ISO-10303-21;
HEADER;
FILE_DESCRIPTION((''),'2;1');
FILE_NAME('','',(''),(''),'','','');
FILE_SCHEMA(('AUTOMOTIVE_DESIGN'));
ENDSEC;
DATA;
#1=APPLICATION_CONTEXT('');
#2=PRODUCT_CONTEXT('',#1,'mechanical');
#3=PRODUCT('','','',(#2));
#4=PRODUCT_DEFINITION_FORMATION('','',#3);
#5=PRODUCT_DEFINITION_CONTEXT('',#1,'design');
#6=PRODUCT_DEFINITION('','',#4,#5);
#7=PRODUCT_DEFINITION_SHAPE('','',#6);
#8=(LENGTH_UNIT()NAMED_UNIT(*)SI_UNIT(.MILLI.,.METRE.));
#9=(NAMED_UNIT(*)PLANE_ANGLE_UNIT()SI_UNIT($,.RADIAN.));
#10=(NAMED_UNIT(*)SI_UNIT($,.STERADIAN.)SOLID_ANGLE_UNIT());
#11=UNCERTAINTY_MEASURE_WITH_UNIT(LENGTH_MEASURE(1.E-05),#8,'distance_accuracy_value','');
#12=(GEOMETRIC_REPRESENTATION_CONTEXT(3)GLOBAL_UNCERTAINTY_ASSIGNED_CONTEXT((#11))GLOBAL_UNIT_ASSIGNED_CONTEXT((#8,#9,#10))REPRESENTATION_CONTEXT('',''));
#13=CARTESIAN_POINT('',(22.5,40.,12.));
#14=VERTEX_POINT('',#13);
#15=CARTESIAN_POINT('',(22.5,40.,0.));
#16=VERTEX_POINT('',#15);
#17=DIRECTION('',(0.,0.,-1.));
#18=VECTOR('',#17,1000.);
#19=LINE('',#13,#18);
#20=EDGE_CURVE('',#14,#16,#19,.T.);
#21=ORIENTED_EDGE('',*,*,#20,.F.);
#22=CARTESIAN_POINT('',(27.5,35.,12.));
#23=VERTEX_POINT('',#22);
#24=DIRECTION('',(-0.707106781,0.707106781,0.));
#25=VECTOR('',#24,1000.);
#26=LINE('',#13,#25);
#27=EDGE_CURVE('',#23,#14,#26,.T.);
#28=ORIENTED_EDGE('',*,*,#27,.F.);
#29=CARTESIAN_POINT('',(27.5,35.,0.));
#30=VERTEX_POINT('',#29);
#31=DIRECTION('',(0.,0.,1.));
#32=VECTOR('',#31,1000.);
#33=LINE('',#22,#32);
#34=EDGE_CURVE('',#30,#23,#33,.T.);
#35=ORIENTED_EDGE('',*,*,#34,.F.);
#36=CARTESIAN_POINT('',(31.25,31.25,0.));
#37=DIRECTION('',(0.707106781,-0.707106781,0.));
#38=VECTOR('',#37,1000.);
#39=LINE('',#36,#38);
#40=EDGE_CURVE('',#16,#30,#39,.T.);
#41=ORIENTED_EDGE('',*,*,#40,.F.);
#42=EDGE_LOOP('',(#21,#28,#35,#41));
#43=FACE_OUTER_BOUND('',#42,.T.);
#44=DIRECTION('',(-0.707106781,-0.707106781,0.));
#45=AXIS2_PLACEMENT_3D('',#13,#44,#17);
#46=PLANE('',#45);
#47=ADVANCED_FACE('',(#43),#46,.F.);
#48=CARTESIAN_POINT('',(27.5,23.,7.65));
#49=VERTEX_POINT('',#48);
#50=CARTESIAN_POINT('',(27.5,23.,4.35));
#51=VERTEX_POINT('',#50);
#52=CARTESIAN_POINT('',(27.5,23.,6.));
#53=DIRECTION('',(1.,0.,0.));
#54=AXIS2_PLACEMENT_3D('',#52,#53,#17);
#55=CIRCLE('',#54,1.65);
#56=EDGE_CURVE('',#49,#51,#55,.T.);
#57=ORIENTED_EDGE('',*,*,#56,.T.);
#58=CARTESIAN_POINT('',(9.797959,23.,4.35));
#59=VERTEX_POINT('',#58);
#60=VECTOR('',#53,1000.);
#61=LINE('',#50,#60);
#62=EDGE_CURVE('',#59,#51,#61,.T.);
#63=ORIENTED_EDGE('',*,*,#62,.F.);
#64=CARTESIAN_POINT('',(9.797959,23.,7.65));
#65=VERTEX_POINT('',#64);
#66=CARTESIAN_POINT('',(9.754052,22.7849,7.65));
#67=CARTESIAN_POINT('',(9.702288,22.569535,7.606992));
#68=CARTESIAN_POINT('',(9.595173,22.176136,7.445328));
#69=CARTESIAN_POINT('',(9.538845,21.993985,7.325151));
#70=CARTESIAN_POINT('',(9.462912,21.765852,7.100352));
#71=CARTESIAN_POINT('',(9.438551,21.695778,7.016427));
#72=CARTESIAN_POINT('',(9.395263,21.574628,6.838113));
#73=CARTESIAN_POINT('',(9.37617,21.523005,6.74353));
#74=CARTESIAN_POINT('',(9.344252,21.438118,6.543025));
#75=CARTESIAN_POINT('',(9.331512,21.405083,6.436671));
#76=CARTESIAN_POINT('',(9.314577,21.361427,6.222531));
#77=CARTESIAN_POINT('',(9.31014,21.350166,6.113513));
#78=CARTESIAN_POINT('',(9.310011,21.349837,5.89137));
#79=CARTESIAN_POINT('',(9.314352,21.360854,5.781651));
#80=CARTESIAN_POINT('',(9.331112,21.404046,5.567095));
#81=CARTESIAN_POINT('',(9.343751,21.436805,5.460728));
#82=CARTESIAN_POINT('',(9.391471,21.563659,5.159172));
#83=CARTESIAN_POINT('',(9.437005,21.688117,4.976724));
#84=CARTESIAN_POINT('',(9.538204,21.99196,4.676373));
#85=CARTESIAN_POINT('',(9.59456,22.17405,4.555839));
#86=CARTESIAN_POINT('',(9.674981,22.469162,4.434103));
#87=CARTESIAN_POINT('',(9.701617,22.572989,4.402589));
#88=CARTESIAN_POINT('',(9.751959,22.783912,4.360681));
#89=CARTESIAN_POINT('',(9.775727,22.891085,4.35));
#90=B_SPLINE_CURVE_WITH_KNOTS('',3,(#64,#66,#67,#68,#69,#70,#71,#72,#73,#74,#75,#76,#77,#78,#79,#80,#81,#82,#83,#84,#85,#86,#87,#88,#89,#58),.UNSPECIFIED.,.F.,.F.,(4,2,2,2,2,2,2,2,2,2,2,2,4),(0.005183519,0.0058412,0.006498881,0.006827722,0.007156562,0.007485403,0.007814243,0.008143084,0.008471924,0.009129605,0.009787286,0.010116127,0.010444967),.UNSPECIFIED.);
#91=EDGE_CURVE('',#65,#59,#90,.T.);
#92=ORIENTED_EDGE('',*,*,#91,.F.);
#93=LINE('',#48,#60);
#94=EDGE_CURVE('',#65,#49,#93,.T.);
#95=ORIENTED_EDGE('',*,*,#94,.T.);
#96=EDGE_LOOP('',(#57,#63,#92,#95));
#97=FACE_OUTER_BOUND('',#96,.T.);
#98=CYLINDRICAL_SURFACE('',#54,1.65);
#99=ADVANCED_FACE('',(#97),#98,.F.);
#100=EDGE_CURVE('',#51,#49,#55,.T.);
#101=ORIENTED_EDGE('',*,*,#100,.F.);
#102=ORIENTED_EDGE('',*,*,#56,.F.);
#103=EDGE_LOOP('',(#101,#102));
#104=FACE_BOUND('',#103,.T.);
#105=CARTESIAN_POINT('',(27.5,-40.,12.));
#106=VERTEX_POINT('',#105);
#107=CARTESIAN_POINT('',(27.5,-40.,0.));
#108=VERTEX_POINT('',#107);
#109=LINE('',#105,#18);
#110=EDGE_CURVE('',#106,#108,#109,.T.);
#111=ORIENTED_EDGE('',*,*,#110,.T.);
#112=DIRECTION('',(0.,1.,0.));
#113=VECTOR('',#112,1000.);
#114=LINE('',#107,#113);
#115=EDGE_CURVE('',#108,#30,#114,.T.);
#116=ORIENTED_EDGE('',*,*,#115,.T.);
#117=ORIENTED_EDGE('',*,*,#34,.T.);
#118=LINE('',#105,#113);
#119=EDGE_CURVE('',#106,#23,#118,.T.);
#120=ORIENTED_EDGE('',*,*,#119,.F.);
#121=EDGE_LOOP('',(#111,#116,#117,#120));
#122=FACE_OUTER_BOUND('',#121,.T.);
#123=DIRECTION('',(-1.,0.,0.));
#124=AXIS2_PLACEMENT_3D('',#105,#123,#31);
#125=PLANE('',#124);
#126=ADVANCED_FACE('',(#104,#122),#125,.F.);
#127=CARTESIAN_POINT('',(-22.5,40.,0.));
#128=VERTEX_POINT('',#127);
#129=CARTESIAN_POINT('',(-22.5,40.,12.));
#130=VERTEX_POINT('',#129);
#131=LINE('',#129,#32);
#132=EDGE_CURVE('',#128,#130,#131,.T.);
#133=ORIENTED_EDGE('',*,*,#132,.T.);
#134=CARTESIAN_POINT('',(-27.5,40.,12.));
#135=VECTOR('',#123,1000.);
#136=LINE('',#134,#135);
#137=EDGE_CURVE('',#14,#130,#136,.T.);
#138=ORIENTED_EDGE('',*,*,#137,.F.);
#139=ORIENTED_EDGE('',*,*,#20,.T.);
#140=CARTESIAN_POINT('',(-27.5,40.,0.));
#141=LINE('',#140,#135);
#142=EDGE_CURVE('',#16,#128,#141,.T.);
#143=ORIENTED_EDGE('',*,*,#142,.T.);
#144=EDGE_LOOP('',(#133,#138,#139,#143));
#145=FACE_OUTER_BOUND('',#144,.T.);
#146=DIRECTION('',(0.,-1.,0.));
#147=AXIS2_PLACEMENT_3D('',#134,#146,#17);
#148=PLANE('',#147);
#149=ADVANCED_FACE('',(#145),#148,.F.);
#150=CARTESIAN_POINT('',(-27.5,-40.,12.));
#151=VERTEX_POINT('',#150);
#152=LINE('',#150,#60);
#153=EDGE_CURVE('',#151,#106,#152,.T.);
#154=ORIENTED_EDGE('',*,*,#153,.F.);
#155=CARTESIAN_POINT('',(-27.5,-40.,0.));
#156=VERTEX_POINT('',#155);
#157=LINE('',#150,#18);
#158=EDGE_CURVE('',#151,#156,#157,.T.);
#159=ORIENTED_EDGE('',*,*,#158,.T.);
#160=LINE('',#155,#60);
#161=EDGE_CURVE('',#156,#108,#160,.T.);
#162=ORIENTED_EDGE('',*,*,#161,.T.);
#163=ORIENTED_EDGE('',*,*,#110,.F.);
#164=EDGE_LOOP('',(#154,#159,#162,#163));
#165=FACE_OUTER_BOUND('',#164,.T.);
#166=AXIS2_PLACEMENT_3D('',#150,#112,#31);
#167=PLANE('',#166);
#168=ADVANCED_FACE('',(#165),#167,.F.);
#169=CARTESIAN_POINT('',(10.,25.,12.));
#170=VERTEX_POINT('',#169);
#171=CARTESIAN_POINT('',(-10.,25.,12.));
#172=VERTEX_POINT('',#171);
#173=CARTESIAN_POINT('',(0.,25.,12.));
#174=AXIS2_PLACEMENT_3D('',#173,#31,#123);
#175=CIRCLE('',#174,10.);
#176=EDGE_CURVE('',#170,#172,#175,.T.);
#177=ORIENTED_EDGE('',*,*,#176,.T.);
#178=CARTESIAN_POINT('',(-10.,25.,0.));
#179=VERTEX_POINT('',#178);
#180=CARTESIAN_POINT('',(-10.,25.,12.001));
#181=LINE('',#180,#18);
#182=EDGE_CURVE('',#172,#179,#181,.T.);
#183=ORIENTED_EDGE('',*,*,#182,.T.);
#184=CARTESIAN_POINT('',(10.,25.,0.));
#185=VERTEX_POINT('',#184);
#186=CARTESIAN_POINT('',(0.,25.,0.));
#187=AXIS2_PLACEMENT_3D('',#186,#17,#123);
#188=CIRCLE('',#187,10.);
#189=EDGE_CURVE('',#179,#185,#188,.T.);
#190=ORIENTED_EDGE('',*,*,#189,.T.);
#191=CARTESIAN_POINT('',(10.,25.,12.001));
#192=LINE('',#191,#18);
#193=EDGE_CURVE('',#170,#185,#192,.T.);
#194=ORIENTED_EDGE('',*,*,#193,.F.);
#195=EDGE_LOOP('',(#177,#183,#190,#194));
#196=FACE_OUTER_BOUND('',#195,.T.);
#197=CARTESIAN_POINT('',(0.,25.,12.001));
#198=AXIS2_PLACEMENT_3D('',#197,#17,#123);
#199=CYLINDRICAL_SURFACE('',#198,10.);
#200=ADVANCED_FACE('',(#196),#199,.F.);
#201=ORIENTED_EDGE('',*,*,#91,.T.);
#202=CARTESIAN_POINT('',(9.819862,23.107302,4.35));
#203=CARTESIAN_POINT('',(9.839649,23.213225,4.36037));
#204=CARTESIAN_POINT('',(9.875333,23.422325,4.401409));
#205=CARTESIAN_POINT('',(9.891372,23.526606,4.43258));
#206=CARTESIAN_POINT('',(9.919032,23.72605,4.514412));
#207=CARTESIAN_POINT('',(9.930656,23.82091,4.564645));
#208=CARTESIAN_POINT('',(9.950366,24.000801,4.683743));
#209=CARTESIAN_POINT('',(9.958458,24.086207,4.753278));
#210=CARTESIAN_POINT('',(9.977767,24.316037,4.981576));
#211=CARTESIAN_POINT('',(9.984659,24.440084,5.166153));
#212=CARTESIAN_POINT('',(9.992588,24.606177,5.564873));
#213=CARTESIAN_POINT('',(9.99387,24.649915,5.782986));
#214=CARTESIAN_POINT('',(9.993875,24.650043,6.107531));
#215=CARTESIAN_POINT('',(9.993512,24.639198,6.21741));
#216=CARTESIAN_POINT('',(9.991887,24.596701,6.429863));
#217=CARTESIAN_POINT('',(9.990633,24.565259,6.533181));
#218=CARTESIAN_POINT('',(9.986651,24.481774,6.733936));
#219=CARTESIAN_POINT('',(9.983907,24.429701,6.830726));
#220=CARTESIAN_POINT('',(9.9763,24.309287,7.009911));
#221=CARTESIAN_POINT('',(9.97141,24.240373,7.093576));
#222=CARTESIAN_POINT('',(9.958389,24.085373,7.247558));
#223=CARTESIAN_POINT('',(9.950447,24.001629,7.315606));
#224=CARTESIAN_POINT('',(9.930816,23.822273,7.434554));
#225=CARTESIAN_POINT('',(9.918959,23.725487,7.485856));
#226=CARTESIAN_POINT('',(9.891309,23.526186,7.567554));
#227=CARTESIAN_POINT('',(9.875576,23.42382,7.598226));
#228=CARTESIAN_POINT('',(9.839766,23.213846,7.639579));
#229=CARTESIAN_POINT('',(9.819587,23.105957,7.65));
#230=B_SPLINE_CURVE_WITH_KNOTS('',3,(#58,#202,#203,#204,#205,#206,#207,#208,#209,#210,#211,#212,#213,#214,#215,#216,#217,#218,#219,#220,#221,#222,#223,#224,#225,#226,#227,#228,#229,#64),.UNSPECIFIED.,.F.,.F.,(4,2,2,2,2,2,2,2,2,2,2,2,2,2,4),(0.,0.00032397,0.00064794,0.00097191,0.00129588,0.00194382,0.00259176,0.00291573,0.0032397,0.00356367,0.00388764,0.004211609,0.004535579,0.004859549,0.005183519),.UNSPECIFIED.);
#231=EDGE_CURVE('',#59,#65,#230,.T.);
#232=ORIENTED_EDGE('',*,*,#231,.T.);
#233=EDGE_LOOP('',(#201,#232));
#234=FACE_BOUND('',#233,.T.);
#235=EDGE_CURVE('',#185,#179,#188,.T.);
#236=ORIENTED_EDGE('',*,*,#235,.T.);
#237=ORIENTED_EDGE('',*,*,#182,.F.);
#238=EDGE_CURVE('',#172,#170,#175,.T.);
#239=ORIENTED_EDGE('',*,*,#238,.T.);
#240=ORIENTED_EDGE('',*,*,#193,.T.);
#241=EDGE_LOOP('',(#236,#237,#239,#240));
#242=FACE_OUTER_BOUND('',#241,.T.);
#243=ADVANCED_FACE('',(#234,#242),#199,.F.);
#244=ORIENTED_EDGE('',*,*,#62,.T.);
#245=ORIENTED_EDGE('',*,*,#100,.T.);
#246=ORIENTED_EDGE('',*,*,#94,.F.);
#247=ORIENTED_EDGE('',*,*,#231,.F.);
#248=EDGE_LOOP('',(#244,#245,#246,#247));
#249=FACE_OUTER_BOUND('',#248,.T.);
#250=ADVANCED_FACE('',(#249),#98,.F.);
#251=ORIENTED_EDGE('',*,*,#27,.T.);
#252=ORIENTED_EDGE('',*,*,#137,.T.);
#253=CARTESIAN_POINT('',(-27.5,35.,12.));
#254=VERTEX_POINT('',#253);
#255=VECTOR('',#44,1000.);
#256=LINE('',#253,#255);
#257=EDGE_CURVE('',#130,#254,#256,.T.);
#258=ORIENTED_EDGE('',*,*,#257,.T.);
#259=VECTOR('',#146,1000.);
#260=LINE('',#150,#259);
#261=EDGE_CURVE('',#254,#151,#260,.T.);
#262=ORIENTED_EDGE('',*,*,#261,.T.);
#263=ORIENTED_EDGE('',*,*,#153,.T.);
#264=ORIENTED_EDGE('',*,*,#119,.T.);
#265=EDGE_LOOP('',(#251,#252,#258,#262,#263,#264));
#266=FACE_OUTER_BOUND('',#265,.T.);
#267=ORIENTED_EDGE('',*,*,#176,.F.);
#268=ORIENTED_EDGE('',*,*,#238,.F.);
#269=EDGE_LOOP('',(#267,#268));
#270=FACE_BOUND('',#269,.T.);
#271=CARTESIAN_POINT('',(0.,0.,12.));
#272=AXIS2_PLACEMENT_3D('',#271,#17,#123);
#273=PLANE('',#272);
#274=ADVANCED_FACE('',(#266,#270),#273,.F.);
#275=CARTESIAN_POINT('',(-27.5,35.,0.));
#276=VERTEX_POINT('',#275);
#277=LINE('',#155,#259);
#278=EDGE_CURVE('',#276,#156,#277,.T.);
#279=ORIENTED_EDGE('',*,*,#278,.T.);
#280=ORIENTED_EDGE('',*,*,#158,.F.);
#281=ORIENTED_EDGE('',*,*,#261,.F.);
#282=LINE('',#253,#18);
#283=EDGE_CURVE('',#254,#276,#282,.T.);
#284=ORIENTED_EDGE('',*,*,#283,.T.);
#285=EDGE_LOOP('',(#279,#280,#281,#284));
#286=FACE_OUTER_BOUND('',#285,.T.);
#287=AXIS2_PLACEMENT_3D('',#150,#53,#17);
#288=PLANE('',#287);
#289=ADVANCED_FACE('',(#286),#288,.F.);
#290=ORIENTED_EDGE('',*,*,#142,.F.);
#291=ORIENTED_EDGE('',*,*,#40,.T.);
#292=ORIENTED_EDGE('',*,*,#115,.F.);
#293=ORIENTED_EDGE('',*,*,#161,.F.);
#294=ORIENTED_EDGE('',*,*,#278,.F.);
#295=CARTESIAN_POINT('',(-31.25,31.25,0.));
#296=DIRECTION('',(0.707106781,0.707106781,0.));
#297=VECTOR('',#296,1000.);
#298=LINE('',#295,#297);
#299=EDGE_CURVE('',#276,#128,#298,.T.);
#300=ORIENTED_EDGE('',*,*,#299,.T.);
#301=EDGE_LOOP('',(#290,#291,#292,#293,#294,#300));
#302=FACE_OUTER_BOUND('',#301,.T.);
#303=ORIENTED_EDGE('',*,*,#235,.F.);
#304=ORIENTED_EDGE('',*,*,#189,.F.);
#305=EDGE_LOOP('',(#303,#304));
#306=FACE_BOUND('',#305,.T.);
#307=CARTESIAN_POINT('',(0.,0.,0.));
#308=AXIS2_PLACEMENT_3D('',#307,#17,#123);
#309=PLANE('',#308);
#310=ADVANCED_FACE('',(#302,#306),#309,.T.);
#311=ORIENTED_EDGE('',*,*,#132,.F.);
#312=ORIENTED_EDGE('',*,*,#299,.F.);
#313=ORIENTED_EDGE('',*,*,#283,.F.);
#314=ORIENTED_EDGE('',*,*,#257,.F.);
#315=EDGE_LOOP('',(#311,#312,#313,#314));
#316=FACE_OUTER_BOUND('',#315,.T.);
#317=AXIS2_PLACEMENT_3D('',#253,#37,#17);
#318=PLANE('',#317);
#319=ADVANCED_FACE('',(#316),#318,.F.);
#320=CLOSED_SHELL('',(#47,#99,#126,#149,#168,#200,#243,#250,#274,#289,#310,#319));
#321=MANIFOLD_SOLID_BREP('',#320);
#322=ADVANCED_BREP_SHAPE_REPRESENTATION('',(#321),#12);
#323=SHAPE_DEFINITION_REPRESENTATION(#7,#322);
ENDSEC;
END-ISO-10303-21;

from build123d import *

# Parameters (mm, degrees)
SKETCH_1_W              = 55
SKETCH_1_H              = 80
EXTRUDE_1_DEPTH         = 12
CUT_EXTRUDE_4_REACH     = 52.002
SKETCH_5_R              = 10
CHAMFER_1_SIZE          = 5
HOLE_WIZARD_M4_1_REACH  = 85.845
HOLE_WIZARD_M4_1_BORE_R = 1.65


with BuildPart() as part:
    # 草图1 → 凸台-拉伸1 (new body)
    with BuildSketch(Plane.XY):
        Rectangle(SKETCH_1_W, SKETCH_1_H)
    extrude(amount=EXTRUDE_1_DEPTH)

    # 草图5 → 切除-拉伸4 (cut, up to next)
    with BuildSketch(Plane(origin=(0, 0, 0), x_dir=(-1, 0, 0), z_dir=(0, 0, -1)), mode=Mode.PRIVATE) as cut_extrude_4_sk1:
        with Locations((0, 25)):
            Circle(SKETCH_5_R)
    cut_extrude_4_tool1 = extrude(cut_extrude_4_sk1.sketch, amount=-CUT_EXTRUDE_4_REACH, mode=Mode.PRIVATE) & part.part
    add(cut_extrude_4_tool1.solids().sort_by_distance((0, 25, 0))[0], mode=Mode.SUBTRACT)

    # 倒角1
    chamfer_1_edges = [part.edges().sort_by_distance(p)[0] for p in [
        (-27.5, 40, 6),
        (27.5, 40, 6),
    ]]
    chamfer(chamfer_1_edges, length=CHAMFER_1_SIZE)

    # M4 螺纹孔1 bore (on position points) → M4 螺纹孔1 (cut, up to next)
    with BuildSketch(Plane(origin=(27.5, 23, 6), x_dir=(0, 0, 1), z_dir=(1, 0, 0)), mode=Mode.PRIVATE) as hole_wizard_m4_1_sk1:
        Circle(HOLE_WIZARD_M4_1_BORE_R)
    hole_wizard_m4_1_tool1 = extrude(hole_wizard_m4_1_sk1.sketch, amount=-HOLE_WIZARD_M4_1_REACH, mode=Mode.PRIVATE) & part.part
    add(hole_wizard_m4_1_tool1.solids().sort_by_distance((27.5, 23, 6))[0], mode=Mode.SUBTRACT)


solid = part.part
